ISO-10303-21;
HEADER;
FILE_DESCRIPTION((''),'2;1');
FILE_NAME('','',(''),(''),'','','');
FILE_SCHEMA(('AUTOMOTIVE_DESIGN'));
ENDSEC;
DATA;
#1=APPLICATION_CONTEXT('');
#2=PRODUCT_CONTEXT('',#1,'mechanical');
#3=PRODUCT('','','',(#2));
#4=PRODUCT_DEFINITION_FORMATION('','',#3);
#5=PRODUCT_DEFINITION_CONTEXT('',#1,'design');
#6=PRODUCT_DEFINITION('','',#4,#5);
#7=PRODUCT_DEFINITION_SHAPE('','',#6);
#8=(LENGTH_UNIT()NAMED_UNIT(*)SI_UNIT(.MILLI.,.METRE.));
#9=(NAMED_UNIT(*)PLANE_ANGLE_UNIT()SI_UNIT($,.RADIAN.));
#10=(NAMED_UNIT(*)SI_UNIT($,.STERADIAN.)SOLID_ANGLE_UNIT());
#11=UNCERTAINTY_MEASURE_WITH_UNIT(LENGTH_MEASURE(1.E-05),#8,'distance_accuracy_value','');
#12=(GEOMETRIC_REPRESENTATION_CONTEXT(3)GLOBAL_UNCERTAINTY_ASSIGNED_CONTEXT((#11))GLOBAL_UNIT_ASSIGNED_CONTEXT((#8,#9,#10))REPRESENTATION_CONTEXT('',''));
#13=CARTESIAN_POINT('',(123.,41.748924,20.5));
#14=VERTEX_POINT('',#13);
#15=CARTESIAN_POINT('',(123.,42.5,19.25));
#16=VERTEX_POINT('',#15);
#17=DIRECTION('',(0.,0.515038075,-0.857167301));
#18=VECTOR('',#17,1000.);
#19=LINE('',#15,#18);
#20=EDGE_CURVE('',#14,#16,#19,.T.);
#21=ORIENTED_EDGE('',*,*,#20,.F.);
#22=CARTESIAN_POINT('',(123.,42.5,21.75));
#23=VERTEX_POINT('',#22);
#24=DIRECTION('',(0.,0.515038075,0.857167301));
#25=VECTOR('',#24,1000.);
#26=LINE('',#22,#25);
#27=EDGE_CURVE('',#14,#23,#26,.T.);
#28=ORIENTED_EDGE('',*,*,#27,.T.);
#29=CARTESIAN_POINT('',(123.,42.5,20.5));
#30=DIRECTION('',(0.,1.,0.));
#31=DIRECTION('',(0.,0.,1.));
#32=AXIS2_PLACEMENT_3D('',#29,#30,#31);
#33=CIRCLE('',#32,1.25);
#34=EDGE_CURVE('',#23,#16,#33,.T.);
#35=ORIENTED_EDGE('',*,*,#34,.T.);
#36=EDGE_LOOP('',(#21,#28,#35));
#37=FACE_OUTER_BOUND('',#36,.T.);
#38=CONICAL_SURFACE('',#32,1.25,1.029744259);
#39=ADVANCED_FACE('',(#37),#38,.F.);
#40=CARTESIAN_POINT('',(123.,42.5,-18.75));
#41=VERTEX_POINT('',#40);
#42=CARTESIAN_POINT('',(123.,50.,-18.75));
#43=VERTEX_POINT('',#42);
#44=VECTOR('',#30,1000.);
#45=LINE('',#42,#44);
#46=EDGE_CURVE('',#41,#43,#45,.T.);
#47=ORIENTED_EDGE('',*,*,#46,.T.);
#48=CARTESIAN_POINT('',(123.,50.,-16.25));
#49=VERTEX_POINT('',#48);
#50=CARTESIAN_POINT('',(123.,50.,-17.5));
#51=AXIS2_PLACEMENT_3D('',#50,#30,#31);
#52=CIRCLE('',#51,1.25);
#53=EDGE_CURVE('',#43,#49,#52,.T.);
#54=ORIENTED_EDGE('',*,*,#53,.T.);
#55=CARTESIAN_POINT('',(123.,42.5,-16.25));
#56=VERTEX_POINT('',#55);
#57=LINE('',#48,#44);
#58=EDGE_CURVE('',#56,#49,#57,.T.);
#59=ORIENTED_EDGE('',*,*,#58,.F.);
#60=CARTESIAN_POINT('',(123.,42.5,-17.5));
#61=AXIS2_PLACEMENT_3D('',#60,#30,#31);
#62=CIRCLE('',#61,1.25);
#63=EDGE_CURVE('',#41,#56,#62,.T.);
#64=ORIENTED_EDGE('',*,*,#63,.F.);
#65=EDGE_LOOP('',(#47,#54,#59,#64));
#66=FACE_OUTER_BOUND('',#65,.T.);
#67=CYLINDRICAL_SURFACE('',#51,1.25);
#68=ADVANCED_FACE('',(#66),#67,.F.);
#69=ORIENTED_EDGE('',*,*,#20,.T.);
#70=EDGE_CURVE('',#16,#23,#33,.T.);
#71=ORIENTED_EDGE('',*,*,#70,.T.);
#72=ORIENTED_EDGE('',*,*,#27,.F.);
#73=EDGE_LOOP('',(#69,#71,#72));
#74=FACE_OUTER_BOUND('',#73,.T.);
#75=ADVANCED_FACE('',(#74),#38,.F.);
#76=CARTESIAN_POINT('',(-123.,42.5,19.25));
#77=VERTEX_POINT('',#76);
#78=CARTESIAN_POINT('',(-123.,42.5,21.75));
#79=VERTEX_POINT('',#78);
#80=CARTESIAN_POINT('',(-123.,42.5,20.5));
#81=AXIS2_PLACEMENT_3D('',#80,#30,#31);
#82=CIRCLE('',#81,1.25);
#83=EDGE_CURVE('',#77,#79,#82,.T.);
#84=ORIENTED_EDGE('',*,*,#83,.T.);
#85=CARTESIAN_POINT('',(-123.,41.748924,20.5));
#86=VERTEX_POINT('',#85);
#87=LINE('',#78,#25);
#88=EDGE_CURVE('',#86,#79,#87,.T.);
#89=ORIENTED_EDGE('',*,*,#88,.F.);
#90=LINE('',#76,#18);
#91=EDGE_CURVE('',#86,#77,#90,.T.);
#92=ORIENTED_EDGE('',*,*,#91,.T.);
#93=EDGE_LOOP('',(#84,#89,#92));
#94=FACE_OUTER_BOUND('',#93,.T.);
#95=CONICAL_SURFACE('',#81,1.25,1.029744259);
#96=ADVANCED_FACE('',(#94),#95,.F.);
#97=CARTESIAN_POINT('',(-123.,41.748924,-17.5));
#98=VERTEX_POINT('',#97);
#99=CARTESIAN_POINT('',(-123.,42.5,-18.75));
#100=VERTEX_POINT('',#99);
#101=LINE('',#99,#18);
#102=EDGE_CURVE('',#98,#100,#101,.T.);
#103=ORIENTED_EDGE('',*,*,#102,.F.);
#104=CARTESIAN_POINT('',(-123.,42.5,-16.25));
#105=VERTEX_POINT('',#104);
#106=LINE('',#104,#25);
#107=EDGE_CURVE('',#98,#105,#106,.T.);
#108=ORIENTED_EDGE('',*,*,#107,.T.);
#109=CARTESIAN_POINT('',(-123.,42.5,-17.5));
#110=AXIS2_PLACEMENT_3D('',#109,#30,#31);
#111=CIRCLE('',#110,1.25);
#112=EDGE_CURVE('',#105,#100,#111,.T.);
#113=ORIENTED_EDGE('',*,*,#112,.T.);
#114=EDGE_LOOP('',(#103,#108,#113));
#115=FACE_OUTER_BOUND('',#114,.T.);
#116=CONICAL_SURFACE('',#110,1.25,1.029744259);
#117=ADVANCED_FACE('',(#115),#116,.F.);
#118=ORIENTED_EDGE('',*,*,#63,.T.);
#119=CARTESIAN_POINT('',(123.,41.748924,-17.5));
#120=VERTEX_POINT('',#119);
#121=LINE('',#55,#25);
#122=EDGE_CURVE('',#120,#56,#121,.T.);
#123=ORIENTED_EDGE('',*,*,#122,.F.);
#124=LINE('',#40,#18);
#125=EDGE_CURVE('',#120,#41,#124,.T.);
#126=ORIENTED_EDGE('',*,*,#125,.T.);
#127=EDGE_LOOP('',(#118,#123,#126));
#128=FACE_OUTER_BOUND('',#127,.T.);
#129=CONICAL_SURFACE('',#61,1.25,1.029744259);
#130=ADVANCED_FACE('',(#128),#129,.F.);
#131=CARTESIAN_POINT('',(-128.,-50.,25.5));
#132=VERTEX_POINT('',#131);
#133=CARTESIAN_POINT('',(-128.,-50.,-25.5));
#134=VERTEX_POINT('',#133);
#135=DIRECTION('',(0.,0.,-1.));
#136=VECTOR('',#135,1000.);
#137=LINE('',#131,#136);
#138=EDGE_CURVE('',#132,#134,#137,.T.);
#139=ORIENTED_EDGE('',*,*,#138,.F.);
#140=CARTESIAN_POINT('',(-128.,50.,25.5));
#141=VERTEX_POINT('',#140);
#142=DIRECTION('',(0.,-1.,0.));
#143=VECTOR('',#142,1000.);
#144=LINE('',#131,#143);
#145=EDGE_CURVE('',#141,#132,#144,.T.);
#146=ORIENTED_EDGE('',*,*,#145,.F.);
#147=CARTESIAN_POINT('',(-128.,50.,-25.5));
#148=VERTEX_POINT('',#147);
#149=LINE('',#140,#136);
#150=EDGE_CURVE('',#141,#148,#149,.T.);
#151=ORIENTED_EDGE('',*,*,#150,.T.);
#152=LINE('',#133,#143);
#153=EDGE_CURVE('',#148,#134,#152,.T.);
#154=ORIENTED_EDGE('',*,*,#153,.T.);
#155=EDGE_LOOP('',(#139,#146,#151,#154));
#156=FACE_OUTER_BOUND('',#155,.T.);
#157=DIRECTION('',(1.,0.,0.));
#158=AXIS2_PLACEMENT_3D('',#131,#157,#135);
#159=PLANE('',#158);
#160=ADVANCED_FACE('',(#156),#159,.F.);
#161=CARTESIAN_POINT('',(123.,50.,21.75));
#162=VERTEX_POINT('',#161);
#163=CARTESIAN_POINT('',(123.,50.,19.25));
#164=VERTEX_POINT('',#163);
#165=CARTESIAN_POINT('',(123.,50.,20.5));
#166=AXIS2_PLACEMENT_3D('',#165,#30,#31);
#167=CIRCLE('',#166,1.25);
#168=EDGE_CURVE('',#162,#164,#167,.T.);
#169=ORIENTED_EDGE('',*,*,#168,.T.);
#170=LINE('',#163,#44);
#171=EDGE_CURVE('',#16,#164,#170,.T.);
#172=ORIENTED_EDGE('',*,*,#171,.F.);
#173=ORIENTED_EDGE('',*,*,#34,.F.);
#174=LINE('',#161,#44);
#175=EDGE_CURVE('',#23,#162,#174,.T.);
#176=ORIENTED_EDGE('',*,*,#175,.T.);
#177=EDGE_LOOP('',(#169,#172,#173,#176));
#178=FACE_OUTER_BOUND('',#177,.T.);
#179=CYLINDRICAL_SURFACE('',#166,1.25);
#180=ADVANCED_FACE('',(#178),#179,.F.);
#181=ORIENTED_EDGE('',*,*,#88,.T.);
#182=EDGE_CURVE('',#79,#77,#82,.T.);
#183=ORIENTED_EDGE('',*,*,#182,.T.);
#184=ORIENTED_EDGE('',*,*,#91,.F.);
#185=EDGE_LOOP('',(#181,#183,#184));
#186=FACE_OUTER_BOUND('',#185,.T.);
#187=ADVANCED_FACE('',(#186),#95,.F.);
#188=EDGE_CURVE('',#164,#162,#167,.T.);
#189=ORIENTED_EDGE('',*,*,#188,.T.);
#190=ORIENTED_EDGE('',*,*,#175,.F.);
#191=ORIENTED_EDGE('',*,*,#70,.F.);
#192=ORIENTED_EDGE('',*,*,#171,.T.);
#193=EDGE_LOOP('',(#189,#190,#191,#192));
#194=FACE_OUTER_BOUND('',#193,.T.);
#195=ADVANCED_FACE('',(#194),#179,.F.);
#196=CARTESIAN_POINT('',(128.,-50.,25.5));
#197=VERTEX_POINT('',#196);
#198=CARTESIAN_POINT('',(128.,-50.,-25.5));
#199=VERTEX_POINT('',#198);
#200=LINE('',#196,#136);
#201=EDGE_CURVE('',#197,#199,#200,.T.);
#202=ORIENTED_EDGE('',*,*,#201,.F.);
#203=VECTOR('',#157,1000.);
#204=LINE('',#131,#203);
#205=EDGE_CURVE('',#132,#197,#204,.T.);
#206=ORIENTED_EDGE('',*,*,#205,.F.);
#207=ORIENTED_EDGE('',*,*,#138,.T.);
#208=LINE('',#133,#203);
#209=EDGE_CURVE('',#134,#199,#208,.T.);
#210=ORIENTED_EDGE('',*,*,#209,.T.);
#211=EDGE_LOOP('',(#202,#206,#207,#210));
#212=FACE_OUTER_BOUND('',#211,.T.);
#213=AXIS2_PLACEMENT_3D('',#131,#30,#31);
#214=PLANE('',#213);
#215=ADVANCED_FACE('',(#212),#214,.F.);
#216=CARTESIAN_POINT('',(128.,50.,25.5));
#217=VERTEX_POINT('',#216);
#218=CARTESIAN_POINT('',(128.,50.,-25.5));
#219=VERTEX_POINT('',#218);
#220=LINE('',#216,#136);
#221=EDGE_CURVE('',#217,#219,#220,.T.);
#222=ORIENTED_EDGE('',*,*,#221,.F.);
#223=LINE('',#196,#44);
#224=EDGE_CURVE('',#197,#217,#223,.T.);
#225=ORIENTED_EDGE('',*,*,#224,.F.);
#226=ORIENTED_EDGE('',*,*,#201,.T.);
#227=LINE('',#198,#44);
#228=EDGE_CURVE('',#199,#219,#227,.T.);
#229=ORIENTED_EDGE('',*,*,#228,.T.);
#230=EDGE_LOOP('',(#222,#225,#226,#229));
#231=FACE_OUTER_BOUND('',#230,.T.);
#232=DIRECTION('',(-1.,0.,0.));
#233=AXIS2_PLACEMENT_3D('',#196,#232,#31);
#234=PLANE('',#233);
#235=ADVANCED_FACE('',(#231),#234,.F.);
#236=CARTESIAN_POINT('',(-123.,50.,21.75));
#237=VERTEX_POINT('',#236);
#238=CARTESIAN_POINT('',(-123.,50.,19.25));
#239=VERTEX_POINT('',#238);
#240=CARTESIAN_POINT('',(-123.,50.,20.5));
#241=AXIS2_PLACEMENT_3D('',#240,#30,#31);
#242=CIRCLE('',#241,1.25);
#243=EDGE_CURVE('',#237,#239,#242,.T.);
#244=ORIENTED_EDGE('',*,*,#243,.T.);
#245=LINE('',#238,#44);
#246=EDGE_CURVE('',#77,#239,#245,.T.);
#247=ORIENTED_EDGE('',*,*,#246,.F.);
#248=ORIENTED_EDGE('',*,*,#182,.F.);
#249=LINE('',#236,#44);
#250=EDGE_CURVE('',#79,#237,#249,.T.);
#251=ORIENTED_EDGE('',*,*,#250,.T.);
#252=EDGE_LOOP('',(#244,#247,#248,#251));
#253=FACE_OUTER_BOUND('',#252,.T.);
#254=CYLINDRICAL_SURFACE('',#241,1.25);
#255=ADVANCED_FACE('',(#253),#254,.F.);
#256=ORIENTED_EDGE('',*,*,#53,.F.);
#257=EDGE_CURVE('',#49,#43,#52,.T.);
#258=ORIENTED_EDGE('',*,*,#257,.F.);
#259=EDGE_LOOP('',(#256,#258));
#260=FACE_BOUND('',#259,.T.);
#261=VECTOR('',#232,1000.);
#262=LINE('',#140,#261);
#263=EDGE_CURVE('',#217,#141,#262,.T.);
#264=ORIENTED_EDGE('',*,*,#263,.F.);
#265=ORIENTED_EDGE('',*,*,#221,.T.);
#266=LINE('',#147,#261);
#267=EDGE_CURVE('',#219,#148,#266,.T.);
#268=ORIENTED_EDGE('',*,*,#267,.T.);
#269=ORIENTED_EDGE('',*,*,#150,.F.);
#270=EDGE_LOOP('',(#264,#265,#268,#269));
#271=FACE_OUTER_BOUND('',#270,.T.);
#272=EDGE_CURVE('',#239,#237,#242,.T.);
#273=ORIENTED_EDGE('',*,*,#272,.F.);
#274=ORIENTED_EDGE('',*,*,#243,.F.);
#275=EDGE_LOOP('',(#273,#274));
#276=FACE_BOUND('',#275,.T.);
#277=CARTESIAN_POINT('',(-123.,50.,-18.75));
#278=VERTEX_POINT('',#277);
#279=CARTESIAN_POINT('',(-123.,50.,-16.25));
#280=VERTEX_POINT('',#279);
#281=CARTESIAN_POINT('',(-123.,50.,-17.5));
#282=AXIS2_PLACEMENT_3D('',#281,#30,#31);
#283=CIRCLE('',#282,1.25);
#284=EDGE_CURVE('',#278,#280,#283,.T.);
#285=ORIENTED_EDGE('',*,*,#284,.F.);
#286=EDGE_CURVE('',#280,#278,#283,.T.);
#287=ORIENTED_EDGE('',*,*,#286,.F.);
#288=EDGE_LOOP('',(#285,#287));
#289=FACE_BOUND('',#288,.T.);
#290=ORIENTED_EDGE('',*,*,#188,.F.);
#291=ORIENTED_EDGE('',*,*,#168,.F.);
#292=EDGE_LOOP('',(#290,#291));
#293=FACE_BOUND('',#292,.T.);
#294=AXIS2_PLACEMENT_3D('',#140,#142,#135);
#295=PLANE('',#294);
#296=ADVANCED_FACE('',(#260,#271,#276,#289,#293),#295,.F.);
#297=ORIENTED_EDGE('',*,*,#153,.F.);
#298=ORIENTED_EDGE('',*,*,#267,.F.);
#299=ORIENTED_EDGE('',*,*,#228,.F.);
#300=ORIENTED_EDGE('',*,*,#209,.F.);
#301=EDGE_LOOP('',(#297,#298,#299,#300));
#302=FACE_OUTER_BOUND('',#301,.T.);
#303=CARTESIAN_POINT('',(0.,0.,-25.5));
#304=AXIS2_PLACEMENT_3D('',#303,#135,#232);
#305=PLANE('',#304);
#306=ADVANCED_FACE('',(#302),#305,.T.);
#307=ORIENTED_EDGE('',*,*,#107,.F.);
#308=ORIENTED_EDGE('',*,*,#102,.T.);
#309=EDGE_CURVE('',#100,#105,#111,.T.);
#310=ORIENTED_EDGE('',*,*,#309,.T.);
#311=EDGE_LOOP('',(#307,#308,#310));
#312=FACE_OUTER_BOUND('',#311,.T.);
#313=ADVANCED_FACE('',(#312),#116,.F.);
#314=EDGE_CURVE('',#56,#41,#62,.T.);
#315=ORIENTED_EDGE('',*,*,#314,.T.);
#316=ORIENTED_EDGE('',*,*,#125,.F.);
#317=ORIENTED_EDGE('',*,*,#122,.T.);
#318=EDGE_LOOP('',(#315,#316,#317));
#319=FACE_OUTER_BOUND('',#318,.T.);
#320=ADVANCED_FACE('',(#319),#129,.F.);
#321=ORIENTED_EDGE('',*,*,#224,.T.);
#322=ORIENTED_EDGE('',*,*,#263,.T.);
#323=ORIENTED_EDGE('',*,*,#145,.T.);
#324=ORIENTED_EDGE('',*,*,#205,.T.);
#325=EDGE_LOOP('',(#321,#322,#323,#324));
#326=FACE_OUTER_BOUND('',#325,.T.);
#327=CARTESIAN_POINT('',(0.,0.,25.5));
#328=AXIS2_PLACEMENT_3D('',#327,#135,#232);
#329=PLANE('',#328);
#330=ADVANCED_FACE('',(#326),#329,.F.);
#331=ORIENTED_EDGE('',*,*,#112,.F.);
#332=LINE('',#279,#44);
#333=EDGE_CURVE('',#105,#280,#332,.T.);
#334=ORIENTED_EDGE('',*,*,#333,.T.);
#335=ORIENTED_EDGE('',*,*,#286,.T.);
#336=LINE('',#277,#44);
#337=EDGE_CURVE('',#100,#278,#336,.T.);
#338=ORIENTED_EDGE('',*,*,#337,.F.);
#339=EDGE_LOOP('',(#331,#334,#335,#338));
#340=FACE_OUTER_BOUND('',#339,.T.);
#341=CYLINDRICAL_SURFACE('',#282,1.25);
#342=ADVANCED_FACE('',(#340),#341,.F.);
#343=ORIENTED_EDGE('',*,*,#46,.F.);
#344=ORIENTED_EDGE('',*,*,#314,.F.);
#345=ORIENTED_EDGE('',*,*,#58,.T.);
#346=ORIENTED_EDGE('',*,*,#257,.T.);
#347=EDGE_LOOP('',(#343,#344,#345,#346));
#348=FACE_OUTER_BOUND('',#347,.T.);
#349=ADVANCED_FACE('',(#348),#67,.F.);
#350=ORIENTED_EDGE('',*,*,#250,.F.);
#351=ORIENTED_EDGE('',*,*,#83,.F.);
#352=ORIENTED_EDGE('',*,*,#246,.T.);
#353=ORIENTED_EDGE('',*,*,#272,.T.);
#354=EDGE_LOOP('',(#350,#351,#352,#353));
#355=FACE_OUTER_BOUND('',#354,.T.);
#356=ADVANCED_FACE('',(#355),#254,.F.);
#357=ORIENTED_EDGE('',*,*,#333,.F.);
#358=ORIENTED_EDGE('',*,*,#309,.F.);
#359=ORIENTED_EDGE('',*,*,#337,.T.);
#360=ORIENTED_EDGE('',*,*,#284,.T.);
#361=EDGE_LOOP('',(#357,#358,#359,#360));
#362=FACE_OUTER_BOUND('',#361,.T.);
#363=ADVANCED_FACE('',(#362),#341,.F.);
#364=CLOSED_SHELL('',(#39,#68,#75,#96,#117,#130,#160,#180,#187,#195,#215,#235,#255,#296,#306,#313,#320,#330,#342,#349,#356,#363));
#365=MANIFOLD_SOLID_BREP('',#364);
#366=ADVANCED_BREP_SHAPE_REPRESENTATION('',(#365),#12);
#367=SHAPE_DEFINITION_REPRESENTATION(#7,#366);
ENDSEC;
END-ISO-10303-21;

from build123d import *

# Parameters (mm, degrees)
SKETCH_1_W             = 256
SKETCH_1_H             = 100
EXTRUDE_1_DEPTH        = 25.5
HOLE_WIZARD_M3_1_D     = 2.5
HOLE_WIZARD_M3_1_DEPTH = 7.5
HOLE_WIZARD_M3_1_TIP   = 0.751075774


with BuildPart() as part:
    # 草图1 → 凸台-拉伸1 (new, symmetric)
    with BuildSketch(Plane.XY):
        Rectangle(SKETCH_1_W, SKETCH_1_H)
    extrude(amount=EXTRUDE_1_DEPTH, both=True)

    # M3 螺纹孔1
    with Locations(Plane(origin=(0, 50, 0), x_dir=(1, 0, 0), z_dir=(0, 1, 0))):
        with Locations((-123, 17.5), (-123, -20.5), (123, 17.5), (123, -20.5)):
            Hole(HOLE_WIZARD_M3_1_D / 2, depth=HOLE_WIZARD_M3_1_DEPTH)
            with Locations((0, 0, -(HOLE_WIZARD_M3_1_DEPTH + HOLE_WIZARD_M3_1_TIP / 2))):  # 118° drill point
                Cone(0, HOLE_WIZARD_M3_1_D / 2, HOLE_WIZARD_M3_1_TIP, mode=Mode.SUBTRACT)


solid = part.part
